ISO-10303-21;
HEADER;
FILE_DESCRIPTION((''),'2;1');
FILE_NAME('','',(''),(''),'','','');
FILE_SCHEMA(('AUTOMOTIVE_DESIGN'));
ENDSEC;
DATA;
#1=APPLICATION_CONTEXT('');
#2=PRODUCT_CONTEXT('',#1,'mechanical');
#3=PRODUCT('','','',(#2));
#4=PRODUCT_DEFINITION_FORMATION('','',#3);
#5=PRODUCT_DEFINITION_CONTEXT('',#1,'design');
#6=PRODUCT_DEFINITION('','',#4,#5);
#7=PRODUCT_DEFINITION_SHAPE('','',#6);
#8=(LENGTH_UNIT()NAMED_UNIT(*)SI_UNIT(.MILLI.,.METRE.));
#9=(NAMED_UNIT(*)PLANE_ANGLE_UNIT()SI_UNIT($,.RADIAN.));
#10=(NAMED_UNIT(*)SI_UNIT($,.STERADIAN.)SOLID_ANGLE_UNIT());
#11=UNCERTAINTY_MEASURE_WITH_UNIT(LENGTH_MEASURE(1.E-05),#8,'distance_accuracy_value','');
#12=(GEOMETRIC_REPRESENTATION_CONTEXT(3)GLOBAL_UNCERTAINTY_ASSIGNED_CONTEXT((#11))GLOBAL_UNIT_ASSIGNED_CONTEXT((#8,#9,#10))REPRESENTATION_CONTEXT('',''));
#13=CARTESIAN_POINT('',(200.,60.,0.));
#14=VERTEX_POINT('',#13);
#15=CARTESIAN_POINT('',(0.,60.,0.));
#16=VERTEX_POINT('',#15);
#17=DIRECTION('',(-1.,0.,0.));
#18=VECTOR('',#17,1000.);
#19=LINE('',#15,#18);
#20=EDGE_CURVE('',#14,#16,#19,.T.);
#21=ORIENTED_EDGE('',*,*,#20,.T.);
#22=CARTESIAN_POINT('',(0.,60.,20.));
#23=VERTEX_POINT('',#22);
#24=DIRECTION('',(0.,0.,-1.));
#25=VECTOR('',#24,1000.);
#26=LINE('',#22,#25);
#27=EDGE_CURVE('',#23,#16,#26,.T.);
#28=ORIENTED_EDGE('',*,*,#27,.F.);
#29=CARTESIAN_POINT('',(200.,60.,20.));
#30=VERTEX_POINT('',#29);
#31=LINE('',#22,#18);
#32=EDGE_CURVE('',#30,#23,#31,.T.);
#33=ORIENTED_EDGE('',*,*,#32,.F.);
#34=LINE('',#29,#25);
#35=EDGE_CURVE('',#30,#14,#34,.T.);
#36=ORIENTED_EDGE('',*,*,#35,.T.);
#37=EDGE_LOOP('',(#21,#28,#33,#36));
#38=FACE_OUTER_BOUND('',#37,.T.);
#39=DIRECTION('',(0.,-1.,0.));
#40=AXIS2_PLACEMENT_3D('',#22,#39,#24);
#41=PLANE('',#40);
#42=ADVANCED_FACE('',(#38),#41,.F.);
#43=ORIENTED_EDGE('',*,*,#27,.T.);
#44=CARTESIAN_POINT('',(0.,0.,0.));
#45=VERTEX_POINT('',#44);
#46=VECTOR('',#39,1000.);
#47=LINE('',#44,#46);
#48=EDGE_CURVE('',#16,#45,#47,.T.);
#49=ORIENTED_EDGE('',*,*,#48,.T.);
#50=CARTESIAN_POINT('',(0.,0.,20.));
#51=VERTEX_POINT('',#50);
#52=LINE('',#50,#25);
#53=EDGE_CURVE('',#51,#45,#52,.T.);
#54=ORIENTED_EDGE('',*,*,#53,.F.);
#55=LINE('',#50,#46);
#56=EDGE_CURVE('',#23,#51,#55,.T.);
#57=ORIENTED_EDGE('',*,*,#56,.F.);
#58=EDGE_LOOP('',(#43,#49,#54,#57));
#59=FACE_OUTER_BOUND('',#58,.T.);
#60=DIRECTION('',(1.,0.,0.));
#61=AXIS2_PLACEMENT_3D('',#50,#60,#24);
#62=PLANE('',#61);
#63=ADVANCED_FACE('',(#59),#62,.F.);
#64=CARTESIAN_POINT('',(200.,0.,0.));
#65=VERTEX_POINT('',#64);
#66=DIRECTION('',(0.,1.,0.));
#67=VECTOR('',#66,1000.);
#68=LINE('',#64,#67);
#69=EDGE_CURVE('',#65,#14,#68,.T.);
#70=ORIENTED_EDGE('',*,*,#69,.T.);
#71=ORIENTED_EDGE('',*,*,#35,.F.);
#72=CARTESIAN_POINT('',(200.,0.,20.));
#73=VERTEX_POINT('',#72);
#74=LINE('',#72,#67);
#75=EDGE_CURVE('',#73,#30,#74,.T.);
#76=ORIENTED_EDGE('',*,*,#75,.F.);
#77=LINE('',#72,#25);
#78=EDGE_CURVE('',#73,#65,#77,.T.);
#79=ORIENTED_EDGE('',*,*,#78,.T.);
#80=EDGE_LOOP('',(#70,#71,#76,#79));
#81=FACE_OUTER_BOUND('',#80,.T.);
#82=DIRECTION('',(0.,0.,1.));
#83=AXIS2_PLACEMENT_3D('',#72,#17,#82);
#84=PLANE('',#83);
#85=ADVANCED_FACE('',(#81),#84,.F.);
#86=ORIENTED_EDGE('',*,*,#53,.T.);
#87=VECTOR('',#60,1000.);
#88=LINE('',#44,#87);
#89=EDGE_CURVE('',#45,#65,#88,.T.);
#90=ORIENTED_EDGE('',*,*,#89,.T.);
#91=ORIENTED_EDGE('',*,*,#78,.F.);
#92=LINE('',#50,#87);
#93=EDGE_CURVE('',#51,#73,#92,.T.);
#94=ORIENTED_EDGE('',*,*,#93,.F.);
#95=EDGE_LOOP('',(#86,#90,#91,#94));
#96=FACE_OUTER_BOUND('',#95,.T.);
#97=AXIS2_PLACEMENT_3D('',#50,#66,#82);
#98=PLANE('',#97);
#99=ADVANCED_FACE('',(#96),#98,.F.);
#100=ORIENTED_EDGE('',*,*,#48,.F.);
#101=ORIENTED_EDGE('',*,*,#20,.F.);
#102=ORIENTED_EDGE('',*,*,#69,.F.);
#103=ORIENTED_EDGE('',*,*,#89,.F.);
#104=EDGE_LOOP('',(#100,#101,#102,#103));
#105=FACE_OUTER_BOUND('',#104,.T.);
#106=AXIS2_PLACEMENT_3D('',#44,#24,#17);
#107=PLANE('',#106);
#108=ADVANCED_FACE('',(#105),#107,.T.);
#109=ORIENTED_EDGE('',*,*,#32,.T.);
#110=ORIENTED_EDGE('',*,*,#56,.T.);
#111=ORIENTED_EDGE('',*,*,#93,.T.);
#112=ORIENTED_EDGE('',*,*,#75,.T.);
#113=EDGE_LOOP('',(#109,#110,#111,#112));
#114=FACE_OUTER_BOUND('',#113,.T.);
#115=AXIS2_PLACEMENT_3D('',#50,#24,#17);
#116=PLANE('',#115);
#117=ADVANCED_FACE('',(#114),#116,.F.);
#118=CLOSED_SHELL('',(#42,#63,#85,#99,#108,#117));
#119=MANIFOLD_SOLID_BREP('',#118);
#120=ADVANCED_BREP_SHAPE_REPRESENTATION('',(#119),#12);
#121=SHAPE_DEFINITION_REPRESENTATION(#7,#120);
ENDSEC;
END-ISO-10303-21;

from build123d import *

# Parameters (mm, degrees)
SKETCH1_W           = 200
SKETCH1_H           = 60
BOSS_EXTRUDE1_DEPTH = 20


with BuildPart() as part:
    # Sketch1 → Boss-Extrude1 (new body)
    with BuildSketch(Plane.XY):
        with Locations((100, 30)):
            Rectangle(SKETCH1_W, SKETCH1_H)
    extrude(amount=BOSS_EXTRUDE1_DEPTH)


solid = part.part
